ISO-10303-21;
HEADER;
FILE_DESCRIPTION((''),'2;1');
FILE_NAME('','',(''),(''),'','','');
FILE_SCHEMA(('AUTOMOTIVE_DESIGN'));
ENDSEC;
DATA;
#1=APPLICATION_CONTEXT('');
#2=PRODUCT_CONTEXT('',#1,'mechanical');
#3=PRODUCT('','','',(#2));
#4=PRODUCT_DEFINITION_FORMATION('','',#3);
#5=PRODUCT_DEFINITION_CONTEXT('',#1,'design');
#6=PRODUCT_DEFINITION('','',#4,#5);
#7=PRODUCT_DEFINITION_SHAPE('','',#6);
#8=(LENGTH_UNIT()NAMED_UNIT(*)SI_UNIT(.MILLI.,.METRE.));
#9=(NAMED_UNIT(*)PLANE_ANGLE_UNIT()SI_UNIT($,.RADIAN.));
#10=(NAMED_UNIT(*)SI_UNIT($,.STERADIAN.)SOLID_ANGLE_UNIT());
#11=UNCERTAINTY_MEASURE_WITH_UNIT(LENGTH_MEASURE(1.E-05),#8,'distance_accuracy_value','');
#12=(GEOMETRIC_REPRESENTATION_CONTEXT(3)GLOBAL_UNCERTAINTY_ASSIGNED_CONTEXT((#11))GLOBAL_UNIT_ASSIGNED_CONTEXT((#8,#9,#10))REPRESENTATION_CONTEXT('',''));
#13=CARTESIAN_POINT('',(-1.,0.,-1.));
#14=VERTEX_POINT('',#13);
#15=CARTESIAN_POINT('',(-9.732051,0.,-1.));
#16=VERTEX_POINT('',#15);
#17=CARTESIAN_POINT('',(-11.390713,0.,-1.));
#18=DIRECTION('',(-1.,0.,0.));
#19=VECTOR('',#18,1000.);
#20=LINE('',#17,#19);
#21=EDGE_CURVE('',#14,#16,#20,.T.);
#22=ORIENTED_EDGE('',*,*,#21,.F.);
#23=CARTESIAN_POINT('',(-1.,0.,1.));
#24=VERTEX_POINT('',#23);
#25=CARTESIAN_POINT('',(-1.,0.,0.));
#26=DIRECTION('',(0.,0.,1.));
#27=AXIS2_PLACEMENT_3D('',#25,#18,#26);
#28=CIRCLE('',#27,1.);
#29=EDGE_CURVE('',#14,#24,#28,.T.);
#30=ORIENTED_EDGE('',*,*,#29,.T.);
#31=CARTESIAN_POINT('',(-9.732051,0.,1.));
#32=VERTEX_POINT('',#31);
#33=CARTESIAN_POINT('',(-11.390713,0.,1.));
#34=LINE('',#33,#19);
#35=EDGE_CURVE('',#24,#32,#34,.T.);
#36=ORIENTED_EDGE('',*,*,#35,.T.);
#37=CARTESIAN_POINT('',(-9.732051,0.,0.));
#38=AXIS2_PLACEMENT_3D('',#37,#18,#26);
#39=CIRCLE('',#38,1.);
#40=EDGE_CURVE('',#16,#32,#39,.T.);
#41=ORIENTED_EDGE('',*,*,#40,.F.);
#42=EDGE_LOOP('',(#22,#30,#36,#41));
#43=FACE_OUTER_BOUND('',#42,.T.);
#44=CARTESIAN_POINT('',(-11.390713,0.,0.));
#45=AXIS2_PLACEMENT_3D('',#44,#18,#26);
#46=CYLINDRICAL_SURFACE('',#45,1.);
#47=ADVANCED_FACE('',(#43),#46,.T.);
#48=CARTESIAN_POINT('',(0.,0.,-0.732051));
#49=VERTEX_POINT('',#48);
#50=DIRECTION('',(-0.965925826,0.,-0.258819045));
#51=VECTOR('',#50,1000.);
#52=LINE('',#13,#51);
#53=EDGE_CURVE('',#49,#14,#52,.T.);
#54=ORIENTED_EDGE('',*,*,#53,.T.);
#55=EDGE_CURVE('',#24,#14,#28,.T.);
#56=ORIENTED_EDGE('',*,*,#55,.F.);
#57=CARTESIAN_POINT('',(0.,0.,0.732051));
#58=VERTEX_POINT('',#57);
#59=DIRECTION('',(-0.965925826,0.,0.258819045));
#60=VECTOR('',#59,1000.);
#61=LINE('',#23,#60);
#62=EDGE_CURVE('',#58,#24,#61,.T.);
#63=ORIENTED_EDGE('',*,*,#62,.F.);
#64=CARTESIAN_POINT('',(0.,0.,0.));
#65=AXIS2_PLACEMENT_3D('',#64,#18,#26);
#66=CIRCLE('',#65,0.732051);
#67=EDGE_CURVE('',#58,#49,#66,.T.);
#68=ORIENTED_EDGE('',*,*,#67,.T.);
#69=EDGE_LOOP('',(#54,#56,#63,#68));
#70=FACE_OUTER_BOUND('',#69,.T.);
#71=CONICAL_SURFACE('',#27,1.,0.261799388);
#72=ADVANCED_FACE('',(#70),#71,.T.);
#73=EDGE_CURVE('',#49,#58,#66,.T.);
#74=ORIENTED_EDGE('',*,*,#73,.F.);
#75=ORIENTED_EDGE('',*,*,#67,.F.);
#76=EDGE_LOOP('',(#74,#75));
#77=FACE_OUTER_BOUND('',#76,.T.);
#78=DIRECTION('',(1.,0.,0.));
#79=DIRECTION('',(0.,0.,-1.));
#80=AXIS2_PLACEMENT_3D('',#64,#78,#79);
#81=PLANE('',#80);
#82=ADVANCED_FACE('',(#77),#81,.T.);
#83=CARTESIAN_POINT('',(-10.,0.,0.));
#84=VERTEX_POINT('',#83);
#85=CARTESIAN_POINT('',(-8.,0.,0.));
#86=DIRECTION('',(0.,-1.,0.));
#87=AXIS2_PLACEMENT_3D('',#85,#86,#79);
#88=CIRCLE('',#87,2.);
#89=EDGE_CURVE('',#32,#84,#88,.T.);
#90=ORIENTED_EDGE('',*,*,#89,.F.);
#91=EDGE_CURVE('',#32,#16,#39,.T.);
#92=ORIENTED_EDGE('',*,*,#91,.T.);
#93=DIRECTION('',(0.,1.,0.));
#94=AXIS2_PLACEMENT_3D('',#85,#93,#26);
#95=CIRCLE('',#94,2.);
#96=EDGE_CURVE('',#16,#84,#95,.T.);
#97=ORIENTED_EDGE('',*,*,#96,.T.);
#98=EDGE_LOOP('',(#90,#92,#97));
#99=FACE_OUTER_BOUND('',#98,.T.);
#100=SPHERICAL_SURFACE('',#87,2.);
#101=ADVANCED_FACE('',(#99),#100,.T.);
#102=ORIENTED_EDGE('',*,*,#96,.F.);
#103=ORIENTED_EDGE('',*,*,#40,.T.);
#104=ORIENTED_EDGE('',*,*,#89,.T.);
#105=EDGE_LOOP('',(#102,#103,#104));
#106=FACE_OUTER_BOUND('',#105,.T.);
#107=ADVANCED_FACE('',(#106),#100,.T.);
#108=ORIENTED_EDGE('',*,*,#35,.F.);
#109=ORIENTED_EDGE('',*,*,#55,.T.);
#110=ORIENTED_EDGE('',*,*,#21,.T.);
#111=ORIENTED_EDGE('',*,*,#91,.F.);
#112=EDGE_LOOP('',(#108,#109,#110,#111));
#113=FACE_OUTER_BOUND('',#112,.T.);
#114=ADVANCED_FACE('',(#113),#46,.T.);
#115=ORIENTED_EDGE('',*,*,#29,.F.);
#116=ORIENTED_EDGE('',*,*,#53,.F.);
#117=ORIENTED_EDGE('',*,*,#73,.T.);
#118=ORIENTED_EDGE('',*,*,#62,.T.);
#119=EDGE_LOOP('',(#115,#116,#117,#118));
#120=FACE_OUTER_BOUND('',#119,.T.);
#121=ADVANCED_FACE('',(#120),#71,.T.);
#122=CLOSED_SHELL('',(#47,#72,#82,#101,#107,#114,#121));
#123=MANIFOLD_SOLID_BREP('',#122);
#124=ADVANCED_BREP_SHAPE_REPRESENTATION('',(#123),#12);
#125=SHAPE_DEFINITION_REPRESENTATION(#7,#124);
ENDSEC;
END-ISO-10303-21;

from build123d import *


with BuildPart() as part:
    # Sketch1 → Revolve1 (revolve)
    with BuildSketch(Plane(origin=(0, 0, 0), x_dir=(1, 0, 0), z_dir=(0, 1, 0))):
        with BuildLine():
            Line((-1, -1), (0, -0.732050808))
            Line((0, -0.732050808), (0, 0))
            Line((0, 0), (-10, 0))
            ThreePointArc((-10, 0), (-9.931851653, -0.51763809), (-9.732050808, -1))
            Line((-9.732050808, -1), (-1, -1))
        make_face()
    revolve(axis=Axis((-11.390713055, 0, 0), (1, 0, 0)))


solid = part.part
